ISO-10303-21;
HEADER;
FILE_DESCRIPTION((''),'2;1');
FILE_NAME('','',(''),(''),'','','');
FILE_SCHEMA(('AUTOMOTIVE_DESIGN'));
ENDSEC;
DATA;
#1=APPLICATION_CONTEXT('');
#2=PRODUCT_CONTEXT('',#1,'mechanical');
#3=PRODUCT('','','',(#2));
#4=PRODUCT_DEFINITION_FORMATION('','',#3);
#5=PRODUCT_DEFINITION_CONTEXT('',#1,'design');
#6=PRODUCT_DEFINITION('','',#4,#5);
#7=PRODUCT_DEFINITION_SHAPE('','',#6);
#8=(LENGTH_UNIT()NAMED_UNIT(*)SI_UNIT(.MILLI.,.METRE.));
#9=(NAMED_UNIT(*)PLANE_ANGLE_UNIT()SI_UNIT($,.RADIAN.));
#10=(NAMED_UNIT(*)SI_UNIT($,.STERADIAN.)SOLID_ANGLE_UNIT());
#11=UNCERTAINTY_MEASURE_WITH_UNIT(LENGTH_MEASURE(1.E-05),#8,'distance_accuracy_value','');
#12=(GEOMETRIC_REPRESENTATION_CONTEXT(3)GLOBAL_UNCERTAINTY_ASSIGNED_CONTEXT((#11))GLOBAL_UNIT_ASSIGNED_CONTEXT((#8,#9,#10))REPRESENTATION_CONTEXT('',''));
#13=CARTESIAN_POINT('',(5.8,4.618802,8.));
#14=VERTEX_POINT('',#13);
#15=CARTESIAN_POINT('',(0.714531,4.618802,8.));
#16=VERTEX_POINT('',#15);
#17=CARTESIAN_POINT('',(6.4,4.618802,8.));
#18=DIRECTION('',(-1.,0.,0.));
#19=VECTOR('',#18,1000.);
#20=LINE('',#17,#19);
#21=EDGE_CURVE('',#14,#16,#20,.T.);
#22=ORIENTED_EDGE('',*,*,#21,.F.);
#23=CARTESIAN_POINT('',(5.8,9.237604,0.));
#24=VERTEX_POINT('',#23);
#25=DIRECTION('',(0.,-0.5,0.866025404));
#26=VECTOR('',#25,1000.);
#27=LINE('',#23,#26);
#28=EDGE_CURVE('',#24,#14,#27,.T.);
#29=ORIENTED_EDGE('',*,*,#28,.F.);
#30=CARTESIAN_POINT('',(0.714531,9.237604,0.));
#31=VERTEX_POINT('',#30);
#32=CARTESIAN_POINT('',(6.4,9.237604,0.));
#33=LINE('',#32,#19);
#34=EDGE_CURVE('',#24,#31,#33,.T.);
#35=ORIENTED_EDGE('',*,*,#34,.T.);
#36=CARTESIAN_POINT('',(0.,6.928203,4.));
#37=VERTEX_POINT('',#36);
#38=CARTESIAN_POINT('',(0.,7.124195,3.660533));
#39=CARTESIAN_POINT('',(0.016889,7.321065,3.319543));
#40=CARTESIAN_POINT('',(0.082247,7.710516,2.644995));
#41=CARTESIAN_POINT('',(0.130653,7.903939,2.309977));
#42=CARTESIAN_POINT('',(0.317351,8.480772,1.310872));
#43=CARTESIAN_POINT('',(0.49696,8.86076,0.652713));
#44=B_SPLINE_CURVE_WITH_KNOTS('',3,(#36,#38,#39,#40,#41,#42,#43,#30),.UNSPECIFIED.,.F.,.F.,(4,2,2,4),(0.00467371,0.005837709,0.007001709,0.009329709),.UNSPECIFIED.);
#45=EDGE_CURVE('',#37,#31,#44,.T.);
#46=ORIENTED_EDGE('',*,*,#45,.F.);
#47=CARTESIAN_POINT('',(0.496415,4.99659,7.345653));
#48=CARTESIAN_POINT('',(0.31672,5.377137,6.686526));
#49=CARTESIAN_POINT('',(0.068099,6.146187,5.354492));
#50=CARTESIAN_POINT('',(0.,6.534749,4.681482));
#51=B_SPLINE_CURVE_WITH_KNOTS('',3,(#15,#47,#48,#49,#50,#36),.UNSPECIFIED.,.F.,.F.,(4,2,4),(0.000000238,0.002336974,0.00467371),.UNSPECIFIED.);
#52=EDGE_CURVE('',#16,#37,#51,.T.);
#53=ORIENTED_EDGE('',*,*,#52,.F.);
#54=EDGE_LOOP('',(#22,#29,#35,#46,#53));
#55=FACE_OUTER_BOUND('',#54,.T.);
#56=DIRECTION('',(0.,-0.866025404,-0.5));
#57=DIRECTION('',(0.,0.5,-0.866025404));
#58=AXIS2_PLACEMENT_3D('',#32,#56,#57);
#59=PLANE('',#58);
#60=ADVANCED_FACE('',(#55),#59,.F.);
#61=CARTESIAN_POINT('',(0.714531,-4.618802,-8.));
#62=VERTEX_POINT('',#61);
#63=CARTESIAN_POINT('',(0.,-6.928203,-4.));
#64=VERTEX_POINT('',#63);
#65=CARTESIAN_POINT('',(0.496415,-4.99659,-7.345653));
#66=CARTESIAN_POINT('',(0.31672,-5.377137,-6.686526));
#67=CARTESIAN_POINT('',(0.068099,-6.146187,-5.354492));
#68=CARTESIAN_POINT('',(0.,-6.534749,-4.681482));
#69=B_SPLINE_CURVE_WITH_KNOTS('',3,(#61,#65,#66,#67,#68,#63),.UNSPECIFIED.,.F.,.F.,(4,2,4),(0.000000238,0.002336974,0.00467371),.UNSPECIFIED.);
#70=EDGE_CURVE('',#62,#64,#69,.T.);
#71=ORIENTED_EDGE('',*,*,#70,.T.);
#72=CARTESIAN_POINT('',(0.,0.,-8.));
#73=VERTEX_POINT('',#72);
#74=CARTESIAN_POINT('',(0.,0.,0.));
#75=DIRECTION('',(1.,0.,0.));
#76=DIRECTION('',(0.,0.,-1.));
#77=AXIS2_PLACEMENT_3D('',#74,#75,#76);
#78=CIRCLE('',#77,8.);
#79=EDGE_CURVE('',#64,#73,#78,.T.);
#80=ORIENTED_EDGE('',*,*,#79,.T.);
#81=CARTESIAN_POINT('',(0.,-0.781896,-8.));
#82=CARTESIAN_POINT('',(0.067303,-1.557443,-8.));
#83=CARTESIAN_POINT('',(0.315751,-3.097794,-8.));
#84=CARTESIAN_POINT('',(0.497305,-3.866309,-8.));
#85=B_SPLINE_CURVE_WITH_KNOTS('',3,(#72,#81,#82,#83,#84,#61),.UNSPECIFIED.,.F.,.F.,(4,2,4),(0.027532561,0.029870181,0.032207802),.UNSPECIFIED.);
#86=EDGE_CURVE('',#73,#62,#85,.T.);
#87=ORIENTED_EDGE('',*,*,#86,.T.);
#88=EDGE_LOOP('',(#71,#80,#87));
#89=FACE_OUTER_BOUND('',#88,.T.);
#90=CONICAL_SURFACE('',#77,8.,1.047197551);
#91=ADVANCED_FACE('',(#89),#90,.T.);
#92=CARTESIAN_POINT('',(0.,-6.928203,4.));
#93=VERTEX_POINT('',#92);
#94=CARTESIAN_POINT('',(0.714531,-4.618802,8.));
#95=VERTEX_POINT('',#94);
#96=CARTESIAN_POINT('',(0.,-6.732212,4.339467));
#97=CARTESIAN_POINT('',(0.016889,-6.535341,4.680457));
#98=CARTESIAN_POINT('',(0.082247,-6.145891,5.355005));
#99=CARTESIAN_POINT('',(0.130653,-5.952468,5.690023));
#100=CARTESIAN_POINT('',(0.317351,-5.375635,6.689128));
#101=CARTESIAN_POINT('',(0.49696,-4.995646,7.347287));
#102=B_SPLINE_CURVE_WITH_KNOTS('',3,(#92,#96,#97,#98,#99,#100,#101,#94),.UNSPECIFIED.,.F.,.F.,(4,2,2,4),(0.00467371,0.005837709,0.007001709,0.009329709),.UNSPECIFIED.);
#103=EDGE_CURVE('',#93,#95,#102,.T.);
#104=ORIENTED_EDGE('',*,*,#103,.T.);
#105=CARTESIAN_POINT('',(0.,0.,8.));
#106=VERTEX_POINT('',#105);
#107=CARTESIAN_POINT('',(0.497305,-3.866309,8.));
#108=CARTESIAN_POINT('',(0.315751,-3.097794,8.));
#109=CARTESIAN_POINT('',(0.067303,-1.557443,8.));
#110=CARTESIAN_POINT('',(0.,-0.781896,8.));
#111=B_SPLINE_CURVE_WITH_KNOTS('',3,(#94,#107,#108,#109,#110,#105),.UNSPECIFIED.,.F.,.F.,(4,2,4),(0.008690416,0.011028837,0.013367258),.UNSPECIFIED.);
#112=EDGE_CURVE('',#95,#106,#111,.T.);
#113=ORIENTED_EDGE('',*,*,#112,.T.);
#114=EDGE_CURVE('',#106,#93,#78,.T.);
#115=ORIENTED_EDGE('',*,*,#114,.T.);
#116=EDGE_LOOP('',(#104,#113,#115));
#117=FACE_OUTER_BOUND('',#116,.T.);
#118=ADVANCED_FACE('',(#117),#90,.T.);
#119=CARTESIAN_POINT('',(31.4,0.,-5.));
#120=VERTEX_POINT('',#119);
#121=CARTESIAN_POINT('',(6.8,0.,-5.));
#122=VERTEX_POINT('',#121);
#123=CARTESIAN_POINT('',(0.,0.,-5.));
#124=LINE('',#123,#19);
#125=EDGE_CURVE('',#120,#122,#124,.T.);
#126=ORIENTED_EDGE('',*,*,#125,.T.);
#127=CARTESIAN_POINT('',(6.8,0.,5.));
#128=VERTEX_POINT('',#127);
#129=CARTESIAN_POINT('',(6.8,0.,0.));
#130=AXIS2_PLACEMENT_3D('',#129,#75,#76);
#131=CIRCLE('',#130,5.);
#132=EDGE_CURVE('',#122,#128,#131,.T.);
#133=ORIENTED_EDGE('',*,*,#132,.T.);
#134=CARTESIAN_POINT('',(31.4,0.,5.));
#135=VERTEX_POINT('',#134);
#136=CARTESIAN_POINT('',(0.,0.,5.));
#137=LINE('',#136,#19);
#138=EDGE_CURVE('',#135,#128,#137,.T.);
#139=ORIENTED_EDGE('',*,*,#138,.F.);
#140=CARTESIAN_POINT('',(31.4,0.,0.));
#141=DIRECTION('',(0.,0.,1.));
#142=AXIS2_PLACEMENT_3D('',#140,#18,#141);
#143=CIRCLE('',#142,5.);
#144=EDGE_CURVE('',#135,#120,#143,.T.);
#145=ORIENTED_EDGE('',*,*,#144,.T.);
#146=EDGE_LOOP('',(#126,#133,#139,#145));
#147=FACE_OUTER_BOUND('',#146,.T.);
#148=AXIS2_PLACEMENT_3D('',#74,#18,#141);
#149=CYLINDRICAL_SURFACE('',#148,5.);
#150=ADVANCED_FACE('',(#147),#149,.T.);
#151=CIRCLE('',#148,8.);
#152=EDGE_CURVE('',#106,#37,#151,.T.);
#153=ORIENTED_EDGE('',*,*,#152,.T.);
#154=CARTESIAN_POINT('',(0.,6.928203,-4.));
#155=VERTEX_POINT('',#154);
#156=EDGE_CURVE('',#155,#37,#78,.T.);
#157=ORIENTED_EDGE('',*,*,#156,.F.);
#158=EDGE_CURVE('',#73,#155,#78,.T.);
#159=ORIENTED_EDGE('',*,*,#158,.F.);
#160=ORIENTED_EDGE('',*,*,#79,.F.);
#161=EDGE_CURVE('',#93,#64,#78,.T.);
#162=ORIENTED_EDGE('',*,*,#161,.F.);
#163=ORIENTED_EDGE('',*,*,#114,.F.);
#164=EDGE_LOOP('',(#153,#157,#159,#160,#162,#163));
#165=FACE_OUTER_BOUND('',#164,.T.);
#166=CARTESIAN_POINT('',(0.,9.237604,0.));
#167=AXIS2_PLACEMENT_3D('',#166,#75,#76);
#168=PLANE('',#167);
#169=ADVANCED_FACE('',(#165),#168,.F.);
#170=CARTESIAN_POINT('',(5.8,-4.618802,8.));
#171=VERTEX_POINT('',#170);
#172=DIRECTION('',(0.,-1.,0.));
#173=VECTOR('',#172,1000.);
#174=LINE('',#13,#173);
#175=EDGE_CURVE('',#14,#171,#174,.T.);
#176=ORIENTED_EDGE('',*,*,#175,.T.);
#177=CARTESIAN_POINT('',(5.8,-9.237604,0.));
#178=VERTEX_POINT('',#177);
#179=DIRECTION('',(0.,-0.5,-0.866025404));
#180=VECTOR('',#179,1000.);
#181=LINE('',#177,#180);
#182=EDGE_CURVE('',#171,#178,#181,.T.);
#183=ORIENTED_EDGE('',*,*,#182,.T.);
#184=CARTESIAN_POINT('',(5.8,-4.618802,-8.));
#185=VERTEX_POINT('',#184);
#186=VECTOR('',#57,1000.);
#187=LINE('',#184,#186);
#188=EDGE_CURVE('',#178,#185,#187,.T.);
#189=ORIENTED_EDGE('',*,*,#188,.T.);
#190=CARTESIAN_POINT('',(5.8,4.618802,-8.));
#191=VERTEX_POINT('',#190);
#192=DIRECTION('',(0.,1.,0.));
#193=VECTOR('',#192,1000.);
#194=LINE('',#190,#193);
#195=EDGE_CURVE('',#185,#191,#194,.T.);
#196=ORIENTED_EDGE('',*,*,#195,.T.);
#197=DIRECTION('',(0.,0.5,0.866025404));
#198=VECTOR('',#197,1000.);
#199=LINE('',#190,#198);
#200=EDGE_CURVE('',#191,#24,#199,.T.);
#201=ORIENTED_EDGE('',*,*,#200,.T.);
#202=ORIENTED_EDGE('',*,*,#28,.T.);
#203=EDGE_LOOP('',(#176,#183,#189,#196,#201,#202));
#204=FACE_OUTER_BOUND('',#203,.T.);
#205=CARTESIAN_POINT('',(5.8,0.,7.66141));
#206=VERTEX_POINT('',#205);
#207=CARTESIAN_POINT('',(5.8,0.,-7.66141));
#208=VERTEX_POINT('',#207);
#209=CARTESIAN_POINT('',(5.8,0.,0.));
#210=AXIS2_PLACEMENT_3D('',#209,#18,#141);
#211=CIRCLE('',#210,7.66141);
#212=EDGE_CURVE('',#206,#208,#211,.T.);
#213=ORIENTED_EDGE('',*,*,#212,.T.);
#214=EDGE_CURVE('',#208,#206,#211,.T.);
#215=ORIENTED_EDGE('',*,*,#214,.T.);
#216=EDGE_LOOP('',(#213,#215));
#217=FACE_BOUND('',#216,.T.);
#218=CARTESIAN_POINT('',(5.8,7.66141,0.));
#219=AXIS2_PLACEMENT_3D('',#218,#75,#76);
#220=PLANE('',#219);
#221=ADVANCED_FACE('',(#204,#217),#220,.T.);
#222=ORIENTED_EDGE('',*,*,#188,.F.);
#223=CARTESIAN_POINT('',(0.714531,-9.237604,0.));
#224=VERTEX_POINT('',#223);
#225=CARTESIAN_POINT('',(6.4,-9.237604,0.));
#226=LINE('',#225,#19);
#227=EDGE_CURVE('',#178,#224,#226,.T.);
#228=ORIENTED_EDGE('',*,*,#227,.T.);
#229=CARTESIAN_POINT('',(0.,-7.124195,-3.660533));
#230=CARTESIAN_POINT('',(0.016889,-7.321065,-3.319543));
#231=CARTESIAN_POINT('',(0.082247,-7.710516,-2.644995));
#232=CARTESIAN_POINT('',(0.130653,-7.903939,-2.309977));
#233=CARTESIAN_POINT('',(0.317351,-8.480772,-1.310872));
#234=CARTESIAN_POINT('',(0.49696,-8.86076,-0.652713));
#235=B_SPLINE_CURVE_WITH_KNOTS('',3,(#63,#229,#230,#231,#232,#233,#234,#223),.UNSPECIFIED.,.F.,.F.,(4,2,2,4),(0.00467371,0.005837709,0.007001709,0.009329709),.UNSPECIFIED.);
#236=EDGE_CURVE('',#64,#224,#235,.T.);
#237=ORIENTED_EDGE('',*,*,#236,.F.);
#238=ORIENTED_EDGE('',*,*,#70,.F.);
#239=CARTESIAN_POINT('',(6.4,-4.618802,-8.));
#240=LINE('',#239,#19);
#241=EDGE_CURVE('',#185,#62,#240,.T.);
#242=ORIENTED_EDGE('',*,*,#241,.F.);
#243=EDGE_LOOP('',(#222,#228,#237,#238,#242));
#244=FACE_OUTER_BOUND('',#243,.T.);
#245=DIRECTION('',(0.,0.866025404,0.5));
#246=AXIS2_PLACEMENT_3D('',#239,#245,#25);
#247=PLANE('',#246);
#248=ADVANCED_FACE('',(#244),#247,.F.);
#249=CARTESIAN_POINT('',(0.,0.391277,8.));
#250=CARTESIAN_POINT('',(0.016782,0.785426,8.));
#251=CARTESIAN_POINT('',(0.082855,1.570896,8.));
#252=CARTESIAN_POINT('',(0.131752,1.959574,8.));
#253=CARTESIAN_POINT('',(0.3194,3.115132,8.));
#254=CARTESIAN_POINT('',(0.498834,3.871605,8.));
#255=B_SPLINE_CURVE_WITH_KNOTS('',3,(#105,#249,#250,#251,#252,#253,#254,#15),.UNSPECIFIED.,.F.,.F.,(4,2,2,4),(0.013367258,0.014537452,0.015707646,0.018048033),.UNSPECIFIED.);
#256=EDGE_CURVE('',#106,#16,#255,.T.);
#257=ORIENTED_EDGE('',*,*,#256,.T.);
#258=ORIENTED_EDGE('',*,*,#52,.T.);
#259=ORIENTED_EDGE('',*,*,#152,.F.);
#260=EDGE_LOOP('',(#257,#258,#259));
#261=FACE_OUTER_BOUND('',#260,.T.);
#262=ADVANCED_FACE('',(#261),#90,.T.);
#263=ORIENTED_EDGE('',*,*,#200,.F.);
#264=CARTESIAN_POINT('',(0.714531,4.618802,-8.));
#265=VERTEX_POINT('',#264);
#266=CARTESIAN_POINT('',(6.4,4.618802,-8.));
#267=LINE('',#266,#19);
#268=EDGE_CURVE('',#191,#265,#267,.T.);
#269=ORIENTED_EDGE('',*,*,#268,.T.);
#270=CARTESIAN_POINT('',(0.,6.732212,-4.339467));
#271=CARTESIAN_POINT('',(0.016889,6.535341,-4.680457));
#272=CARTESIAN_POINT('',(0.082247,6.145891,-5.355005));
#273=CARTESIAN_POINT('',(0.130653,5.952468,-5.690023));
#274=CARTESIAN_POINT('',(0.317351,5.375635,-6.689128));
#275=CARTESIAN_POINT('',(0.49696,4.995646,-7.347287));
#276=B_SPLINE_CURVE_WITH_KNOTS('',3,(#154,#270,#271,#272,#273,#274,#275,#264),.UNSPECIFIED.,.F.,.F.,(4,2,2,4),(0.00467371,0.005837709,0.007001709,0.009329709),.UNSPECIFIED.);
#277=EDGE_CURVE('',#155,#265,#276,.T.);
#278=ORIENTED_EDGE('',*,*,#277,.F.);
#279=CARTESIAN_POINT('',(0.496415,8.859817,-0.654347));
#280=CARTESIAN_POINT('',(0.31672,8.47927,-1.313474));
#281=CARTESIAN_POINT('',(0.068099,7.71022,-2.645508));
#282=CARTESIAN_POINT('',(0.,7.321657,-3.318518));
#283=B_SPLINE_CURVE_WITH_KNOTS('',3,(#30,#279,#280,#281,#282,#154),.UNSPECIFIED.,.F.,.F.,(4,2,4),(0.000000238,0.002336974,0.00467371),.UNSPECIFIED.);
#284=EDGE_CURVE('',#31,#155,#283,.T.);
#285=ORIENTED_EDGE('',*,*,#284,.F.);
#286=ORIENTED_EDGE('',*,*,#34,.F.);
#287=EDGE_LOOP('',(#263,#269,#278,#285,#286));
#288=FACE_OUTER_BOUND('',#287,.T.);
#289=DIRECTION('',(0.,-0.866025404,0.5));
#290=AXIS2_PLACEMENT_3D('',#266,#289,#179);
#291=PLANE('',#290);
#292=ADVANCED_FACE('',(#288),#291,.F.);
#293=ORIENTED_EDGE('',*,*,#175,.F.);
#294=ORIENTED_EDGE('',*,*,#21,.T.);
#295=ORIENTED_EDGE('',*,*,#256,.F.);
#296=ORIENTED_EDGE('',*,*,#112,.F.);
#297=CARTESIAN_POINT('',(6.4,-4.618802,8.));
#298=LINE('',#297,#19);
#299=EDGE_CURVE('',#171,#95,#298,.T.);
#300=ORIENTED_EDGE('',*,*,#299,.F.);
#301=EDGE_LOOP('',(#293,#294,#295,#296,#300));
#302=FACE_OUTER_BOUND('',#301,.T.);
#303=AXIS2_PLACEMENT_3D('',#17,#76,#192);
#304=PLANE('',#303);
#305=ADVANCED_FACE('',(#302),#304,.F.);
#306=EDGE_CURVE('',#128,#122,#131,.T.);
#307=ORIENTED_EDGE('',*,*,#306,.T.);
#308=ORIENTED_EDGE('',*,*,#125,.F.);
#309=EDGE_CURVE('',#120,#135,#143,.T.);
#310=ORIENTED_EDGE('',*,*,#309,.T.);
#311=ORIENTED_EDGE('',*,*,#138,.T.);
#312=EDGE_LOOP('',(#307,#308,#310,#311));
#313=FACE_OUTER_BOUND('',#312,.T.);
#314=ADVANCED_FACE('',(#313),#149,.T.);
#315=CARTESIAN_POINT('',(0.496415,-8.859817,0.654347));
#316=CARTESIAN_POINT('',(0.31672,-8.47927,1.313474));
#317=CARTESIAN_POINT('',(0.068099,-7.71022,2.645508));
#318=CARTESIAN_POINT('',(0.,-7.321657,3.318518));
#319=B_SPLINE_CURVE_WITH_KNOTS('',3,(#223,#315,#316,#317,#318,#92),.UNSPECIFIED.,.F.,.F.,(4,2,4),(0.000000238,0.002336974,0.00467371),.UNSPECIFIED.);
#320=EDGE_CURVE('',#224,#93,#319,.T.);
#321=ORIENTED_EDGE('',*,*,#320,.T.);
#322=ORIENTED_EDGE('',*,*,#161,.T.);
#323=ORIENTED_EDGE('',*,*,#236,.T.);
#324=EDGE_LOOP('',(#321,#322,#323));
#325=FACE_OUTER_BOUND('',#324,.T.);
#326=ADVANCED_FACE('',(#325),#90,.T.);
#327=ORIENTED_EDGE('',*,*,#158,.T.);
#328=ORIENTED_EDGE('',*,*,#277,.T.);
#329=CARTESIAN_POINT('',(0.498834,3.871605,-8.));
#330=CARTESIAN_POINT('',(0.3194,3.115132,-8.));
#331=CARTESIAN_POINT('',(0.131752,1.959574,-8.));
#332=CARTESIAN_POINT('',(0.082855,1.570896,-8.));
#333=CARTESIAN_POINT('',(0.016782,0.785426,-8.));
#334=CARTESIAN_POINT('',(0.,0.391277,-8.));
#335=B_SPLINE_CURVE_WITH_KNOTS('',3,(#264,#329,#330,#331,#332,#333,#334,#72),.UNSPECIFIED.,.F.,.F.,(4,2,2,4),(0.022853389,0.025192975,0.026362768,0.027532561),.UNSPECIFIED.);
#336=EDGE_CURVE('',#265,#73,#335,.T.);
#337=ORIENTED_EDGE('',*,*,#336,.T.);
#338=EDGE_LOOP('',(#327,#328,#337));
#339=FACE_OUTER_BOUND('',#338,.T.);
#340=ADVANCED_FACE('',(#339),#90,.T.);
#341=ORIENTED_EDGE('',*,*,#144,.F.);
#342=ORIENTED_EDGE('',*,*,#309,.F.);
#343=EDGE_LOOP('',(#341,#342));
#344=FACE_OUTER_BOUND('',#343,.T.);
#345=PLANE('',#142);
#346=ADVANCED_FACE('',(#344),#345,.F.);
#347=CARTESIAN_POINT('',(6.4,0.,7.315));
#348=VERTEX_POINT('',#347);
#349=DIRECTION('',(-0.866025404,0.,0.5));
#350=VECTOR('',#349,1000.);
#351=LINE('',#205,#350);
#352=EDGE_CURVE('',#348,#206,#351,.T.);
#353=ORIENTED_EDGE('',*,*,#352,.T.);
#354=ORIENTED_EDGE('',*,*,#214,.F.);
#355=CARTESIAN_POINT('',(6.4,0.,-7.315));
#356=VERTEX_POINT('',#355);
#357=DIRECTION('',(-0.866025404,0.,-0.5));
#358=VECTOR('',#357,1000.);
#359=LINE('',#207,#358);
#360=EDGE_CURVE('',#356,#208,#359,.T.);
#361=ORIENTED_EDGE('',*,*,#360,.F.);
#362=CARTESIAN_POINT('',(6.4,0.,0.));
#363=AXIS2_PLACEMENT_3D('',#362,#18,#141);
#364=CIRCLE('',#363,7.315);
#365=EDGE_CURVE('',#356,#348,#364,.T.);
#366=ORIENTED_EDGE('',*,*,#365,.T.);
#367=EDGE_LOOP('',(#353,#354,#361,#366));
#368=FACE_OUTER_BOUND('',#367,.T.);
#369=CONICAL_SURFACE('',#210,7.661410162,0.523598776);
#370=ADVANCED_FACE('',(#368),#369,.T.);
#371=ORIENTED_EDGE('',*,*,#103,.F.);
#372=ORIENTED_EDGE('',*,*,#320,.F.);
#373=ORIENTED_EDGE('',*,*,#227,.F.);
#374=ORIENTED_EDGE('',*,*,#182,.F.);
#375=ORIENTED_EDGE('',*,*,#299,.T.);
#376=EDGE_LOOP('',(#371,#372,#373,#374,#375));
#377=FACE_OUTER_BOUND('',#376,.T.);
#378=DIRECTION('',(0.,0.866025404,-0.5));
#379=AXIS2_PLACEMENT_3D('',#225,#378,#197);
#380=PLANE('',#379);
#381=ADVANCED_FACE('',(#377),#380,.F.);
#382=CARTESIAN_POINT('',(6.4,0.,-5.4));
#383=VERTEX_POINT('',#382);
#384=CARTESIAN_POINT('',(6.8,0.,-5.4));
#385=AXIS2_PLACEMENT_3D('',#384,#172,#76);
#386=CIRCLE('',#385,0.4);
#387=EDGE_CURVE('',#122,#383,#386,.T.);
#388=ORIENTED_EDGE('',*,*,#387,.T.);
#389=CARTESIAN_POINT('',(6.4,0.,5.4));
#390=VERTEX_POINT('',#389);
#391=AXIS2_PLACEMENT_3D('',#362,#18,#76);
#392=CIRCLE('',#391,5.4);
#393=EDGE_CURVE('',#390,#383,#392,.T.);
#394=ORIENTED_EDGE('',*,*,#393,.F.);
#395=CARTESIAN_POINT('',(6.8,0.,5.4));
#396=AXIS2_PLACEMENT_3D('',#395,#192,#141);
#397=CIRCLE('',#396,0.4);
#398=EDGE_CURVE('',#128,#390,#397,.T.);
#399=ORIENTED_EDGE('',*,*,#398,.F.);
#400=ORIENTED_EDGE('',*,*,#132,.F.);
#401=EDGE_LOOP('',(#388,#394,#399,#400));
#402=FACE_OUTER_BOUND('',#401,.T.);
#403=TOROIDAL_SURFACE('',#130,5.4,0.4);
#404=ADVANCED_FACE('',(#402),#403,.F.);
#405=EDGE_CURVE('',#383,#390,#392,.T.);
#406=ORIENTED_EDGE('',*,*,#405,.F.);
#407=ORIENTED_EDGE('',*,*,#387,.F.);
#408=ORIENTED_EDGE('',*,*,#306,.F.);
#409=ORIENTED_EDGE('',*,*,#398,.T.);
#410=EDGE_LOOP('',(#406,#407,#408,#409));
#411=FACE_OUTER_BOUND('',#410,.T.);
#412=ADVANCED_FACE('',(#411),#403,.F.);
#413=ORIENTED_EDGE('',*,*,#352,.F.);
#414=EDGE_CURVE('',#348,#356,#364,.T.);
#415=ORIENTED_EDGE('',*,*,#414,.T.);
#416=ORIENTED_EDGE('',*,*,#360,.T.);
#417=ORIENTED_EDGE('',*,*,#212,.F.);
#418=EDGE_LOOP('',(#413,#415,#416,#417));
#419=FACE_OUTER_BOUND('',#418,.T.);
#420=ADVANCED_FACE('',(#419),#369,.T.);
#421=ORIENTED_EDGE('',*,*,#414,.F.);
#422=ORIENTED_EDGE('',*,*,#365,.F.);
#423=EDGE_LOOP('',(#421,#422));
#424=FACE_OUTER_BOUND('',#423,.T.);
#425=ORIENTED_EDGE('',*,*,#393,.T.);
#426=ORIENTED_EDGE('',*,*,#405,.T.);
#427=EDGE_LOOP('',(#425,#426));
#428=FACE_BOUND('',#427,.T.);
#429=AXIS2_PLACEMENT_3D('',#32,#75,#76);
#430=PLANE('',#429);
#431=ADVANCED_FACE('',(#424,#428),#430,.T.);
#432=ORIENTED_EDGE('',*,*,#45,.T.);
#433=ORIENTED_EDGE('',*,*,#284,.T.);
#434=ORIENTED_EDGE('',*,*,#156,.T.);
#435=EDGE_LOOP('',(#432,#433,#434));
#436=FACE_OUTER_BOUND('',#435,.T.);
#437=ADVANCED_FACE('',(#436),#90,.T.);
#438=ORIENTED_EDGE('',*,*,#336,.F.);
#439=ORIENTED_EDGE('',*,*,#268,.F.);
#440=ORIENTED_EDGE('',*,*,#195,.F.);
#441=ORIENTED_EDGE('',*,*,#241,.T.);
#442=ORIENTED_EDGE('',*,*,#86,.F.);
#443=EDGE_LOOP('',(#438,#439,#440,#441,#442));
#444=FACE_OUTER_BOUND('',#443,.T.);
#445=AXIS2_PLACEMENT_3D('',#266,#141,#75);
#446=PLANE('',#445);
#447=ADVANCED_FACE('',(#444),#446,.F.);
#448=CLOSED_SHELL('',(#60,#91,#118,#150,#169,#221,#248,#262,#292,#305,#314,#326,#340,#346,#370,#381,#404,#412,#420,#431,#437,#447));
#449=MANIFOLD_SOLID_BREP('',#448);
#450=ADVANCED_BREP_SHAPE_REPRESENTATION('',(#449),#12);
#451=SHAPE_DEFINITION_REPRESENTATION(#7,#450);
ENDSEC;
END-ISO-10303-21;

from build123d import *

# Parameters (mm, degrees)
EXTRUDE_387_DEPTH = 6.4
FILLET_1280_R     = 0.4


with BuildPart() as part:
    # 草图1 → Extrude 387 (new body)
    with BuildSketch(Plane(origin=(0, 0, 0), x_dir=(0, 0, -1), z_dir=(1, 0, 0))):
        Polygon((8, 4.618802154), (8, -4.618802154), (0, -9.237604307), (-8, -4.618802154), (-8, 4.618802154), (0, 9.237604307), align=None)
    extrude(amount=EXTRUDE_387_DEPTH)

    # 草图2 → 凸台-旋转1 (revolve)
    with BuildSketch(Plane.XY, mode=Mode.PRIVATE) as revolve_1_sk:
        Polygon((0, 0), (31.4, 0), (31.4, 3.701), (31.4, 5), (16.4, 5), (0, 5), align=None)
    revolve(revolve_1_sk.sketch.rotate(Axis((0, 0, 0), (1, 0, 0)), 90), axis=Axis((0, 0, 0), (1, 0, 0)))

    # 草图3 → 切除-旋转1 (revolve, cut)
    with BuildSketch(Plane.XY):
        Polygon((0, 8), (3.601282526, 14.237604307), (3.601282526, 19.237604307), (-10, 19.237604307), (-10, 8), align=None)
    revolve(axis=Axis((0, 0, 0), (1, 0, 0)), mode=Mode.SUBTRACT)

    # 草图4 → 切除-旋转3 (revolve, cut)
    with BuildSketch(Plane.XY, mode=Mode.PRIVATE) as cut_revolve_3_sk:
        Polygon((6.4, 7.315), (5.8, 7.661410162), (5.8, 9.237604307), (6.4, 9.237604307), align=None)
    revolve(cut_revolve_3_sk.sketch.rotate(Axis((0, 0, 0), (1, 0, 0)), 90), axis=Axis((0, 0, 0), (1, 0, 0)), mode=Mode.SUBTRACT)

    # Fillet 1280
    fillet_1280_edges = [part.edges().sort_by_distance(p)[0] for p in [
        (6.4, 0, -5),
    ]]
    fillet(fillet_1280_edges, radius=FILLET_1280_R)


solid = part.part
